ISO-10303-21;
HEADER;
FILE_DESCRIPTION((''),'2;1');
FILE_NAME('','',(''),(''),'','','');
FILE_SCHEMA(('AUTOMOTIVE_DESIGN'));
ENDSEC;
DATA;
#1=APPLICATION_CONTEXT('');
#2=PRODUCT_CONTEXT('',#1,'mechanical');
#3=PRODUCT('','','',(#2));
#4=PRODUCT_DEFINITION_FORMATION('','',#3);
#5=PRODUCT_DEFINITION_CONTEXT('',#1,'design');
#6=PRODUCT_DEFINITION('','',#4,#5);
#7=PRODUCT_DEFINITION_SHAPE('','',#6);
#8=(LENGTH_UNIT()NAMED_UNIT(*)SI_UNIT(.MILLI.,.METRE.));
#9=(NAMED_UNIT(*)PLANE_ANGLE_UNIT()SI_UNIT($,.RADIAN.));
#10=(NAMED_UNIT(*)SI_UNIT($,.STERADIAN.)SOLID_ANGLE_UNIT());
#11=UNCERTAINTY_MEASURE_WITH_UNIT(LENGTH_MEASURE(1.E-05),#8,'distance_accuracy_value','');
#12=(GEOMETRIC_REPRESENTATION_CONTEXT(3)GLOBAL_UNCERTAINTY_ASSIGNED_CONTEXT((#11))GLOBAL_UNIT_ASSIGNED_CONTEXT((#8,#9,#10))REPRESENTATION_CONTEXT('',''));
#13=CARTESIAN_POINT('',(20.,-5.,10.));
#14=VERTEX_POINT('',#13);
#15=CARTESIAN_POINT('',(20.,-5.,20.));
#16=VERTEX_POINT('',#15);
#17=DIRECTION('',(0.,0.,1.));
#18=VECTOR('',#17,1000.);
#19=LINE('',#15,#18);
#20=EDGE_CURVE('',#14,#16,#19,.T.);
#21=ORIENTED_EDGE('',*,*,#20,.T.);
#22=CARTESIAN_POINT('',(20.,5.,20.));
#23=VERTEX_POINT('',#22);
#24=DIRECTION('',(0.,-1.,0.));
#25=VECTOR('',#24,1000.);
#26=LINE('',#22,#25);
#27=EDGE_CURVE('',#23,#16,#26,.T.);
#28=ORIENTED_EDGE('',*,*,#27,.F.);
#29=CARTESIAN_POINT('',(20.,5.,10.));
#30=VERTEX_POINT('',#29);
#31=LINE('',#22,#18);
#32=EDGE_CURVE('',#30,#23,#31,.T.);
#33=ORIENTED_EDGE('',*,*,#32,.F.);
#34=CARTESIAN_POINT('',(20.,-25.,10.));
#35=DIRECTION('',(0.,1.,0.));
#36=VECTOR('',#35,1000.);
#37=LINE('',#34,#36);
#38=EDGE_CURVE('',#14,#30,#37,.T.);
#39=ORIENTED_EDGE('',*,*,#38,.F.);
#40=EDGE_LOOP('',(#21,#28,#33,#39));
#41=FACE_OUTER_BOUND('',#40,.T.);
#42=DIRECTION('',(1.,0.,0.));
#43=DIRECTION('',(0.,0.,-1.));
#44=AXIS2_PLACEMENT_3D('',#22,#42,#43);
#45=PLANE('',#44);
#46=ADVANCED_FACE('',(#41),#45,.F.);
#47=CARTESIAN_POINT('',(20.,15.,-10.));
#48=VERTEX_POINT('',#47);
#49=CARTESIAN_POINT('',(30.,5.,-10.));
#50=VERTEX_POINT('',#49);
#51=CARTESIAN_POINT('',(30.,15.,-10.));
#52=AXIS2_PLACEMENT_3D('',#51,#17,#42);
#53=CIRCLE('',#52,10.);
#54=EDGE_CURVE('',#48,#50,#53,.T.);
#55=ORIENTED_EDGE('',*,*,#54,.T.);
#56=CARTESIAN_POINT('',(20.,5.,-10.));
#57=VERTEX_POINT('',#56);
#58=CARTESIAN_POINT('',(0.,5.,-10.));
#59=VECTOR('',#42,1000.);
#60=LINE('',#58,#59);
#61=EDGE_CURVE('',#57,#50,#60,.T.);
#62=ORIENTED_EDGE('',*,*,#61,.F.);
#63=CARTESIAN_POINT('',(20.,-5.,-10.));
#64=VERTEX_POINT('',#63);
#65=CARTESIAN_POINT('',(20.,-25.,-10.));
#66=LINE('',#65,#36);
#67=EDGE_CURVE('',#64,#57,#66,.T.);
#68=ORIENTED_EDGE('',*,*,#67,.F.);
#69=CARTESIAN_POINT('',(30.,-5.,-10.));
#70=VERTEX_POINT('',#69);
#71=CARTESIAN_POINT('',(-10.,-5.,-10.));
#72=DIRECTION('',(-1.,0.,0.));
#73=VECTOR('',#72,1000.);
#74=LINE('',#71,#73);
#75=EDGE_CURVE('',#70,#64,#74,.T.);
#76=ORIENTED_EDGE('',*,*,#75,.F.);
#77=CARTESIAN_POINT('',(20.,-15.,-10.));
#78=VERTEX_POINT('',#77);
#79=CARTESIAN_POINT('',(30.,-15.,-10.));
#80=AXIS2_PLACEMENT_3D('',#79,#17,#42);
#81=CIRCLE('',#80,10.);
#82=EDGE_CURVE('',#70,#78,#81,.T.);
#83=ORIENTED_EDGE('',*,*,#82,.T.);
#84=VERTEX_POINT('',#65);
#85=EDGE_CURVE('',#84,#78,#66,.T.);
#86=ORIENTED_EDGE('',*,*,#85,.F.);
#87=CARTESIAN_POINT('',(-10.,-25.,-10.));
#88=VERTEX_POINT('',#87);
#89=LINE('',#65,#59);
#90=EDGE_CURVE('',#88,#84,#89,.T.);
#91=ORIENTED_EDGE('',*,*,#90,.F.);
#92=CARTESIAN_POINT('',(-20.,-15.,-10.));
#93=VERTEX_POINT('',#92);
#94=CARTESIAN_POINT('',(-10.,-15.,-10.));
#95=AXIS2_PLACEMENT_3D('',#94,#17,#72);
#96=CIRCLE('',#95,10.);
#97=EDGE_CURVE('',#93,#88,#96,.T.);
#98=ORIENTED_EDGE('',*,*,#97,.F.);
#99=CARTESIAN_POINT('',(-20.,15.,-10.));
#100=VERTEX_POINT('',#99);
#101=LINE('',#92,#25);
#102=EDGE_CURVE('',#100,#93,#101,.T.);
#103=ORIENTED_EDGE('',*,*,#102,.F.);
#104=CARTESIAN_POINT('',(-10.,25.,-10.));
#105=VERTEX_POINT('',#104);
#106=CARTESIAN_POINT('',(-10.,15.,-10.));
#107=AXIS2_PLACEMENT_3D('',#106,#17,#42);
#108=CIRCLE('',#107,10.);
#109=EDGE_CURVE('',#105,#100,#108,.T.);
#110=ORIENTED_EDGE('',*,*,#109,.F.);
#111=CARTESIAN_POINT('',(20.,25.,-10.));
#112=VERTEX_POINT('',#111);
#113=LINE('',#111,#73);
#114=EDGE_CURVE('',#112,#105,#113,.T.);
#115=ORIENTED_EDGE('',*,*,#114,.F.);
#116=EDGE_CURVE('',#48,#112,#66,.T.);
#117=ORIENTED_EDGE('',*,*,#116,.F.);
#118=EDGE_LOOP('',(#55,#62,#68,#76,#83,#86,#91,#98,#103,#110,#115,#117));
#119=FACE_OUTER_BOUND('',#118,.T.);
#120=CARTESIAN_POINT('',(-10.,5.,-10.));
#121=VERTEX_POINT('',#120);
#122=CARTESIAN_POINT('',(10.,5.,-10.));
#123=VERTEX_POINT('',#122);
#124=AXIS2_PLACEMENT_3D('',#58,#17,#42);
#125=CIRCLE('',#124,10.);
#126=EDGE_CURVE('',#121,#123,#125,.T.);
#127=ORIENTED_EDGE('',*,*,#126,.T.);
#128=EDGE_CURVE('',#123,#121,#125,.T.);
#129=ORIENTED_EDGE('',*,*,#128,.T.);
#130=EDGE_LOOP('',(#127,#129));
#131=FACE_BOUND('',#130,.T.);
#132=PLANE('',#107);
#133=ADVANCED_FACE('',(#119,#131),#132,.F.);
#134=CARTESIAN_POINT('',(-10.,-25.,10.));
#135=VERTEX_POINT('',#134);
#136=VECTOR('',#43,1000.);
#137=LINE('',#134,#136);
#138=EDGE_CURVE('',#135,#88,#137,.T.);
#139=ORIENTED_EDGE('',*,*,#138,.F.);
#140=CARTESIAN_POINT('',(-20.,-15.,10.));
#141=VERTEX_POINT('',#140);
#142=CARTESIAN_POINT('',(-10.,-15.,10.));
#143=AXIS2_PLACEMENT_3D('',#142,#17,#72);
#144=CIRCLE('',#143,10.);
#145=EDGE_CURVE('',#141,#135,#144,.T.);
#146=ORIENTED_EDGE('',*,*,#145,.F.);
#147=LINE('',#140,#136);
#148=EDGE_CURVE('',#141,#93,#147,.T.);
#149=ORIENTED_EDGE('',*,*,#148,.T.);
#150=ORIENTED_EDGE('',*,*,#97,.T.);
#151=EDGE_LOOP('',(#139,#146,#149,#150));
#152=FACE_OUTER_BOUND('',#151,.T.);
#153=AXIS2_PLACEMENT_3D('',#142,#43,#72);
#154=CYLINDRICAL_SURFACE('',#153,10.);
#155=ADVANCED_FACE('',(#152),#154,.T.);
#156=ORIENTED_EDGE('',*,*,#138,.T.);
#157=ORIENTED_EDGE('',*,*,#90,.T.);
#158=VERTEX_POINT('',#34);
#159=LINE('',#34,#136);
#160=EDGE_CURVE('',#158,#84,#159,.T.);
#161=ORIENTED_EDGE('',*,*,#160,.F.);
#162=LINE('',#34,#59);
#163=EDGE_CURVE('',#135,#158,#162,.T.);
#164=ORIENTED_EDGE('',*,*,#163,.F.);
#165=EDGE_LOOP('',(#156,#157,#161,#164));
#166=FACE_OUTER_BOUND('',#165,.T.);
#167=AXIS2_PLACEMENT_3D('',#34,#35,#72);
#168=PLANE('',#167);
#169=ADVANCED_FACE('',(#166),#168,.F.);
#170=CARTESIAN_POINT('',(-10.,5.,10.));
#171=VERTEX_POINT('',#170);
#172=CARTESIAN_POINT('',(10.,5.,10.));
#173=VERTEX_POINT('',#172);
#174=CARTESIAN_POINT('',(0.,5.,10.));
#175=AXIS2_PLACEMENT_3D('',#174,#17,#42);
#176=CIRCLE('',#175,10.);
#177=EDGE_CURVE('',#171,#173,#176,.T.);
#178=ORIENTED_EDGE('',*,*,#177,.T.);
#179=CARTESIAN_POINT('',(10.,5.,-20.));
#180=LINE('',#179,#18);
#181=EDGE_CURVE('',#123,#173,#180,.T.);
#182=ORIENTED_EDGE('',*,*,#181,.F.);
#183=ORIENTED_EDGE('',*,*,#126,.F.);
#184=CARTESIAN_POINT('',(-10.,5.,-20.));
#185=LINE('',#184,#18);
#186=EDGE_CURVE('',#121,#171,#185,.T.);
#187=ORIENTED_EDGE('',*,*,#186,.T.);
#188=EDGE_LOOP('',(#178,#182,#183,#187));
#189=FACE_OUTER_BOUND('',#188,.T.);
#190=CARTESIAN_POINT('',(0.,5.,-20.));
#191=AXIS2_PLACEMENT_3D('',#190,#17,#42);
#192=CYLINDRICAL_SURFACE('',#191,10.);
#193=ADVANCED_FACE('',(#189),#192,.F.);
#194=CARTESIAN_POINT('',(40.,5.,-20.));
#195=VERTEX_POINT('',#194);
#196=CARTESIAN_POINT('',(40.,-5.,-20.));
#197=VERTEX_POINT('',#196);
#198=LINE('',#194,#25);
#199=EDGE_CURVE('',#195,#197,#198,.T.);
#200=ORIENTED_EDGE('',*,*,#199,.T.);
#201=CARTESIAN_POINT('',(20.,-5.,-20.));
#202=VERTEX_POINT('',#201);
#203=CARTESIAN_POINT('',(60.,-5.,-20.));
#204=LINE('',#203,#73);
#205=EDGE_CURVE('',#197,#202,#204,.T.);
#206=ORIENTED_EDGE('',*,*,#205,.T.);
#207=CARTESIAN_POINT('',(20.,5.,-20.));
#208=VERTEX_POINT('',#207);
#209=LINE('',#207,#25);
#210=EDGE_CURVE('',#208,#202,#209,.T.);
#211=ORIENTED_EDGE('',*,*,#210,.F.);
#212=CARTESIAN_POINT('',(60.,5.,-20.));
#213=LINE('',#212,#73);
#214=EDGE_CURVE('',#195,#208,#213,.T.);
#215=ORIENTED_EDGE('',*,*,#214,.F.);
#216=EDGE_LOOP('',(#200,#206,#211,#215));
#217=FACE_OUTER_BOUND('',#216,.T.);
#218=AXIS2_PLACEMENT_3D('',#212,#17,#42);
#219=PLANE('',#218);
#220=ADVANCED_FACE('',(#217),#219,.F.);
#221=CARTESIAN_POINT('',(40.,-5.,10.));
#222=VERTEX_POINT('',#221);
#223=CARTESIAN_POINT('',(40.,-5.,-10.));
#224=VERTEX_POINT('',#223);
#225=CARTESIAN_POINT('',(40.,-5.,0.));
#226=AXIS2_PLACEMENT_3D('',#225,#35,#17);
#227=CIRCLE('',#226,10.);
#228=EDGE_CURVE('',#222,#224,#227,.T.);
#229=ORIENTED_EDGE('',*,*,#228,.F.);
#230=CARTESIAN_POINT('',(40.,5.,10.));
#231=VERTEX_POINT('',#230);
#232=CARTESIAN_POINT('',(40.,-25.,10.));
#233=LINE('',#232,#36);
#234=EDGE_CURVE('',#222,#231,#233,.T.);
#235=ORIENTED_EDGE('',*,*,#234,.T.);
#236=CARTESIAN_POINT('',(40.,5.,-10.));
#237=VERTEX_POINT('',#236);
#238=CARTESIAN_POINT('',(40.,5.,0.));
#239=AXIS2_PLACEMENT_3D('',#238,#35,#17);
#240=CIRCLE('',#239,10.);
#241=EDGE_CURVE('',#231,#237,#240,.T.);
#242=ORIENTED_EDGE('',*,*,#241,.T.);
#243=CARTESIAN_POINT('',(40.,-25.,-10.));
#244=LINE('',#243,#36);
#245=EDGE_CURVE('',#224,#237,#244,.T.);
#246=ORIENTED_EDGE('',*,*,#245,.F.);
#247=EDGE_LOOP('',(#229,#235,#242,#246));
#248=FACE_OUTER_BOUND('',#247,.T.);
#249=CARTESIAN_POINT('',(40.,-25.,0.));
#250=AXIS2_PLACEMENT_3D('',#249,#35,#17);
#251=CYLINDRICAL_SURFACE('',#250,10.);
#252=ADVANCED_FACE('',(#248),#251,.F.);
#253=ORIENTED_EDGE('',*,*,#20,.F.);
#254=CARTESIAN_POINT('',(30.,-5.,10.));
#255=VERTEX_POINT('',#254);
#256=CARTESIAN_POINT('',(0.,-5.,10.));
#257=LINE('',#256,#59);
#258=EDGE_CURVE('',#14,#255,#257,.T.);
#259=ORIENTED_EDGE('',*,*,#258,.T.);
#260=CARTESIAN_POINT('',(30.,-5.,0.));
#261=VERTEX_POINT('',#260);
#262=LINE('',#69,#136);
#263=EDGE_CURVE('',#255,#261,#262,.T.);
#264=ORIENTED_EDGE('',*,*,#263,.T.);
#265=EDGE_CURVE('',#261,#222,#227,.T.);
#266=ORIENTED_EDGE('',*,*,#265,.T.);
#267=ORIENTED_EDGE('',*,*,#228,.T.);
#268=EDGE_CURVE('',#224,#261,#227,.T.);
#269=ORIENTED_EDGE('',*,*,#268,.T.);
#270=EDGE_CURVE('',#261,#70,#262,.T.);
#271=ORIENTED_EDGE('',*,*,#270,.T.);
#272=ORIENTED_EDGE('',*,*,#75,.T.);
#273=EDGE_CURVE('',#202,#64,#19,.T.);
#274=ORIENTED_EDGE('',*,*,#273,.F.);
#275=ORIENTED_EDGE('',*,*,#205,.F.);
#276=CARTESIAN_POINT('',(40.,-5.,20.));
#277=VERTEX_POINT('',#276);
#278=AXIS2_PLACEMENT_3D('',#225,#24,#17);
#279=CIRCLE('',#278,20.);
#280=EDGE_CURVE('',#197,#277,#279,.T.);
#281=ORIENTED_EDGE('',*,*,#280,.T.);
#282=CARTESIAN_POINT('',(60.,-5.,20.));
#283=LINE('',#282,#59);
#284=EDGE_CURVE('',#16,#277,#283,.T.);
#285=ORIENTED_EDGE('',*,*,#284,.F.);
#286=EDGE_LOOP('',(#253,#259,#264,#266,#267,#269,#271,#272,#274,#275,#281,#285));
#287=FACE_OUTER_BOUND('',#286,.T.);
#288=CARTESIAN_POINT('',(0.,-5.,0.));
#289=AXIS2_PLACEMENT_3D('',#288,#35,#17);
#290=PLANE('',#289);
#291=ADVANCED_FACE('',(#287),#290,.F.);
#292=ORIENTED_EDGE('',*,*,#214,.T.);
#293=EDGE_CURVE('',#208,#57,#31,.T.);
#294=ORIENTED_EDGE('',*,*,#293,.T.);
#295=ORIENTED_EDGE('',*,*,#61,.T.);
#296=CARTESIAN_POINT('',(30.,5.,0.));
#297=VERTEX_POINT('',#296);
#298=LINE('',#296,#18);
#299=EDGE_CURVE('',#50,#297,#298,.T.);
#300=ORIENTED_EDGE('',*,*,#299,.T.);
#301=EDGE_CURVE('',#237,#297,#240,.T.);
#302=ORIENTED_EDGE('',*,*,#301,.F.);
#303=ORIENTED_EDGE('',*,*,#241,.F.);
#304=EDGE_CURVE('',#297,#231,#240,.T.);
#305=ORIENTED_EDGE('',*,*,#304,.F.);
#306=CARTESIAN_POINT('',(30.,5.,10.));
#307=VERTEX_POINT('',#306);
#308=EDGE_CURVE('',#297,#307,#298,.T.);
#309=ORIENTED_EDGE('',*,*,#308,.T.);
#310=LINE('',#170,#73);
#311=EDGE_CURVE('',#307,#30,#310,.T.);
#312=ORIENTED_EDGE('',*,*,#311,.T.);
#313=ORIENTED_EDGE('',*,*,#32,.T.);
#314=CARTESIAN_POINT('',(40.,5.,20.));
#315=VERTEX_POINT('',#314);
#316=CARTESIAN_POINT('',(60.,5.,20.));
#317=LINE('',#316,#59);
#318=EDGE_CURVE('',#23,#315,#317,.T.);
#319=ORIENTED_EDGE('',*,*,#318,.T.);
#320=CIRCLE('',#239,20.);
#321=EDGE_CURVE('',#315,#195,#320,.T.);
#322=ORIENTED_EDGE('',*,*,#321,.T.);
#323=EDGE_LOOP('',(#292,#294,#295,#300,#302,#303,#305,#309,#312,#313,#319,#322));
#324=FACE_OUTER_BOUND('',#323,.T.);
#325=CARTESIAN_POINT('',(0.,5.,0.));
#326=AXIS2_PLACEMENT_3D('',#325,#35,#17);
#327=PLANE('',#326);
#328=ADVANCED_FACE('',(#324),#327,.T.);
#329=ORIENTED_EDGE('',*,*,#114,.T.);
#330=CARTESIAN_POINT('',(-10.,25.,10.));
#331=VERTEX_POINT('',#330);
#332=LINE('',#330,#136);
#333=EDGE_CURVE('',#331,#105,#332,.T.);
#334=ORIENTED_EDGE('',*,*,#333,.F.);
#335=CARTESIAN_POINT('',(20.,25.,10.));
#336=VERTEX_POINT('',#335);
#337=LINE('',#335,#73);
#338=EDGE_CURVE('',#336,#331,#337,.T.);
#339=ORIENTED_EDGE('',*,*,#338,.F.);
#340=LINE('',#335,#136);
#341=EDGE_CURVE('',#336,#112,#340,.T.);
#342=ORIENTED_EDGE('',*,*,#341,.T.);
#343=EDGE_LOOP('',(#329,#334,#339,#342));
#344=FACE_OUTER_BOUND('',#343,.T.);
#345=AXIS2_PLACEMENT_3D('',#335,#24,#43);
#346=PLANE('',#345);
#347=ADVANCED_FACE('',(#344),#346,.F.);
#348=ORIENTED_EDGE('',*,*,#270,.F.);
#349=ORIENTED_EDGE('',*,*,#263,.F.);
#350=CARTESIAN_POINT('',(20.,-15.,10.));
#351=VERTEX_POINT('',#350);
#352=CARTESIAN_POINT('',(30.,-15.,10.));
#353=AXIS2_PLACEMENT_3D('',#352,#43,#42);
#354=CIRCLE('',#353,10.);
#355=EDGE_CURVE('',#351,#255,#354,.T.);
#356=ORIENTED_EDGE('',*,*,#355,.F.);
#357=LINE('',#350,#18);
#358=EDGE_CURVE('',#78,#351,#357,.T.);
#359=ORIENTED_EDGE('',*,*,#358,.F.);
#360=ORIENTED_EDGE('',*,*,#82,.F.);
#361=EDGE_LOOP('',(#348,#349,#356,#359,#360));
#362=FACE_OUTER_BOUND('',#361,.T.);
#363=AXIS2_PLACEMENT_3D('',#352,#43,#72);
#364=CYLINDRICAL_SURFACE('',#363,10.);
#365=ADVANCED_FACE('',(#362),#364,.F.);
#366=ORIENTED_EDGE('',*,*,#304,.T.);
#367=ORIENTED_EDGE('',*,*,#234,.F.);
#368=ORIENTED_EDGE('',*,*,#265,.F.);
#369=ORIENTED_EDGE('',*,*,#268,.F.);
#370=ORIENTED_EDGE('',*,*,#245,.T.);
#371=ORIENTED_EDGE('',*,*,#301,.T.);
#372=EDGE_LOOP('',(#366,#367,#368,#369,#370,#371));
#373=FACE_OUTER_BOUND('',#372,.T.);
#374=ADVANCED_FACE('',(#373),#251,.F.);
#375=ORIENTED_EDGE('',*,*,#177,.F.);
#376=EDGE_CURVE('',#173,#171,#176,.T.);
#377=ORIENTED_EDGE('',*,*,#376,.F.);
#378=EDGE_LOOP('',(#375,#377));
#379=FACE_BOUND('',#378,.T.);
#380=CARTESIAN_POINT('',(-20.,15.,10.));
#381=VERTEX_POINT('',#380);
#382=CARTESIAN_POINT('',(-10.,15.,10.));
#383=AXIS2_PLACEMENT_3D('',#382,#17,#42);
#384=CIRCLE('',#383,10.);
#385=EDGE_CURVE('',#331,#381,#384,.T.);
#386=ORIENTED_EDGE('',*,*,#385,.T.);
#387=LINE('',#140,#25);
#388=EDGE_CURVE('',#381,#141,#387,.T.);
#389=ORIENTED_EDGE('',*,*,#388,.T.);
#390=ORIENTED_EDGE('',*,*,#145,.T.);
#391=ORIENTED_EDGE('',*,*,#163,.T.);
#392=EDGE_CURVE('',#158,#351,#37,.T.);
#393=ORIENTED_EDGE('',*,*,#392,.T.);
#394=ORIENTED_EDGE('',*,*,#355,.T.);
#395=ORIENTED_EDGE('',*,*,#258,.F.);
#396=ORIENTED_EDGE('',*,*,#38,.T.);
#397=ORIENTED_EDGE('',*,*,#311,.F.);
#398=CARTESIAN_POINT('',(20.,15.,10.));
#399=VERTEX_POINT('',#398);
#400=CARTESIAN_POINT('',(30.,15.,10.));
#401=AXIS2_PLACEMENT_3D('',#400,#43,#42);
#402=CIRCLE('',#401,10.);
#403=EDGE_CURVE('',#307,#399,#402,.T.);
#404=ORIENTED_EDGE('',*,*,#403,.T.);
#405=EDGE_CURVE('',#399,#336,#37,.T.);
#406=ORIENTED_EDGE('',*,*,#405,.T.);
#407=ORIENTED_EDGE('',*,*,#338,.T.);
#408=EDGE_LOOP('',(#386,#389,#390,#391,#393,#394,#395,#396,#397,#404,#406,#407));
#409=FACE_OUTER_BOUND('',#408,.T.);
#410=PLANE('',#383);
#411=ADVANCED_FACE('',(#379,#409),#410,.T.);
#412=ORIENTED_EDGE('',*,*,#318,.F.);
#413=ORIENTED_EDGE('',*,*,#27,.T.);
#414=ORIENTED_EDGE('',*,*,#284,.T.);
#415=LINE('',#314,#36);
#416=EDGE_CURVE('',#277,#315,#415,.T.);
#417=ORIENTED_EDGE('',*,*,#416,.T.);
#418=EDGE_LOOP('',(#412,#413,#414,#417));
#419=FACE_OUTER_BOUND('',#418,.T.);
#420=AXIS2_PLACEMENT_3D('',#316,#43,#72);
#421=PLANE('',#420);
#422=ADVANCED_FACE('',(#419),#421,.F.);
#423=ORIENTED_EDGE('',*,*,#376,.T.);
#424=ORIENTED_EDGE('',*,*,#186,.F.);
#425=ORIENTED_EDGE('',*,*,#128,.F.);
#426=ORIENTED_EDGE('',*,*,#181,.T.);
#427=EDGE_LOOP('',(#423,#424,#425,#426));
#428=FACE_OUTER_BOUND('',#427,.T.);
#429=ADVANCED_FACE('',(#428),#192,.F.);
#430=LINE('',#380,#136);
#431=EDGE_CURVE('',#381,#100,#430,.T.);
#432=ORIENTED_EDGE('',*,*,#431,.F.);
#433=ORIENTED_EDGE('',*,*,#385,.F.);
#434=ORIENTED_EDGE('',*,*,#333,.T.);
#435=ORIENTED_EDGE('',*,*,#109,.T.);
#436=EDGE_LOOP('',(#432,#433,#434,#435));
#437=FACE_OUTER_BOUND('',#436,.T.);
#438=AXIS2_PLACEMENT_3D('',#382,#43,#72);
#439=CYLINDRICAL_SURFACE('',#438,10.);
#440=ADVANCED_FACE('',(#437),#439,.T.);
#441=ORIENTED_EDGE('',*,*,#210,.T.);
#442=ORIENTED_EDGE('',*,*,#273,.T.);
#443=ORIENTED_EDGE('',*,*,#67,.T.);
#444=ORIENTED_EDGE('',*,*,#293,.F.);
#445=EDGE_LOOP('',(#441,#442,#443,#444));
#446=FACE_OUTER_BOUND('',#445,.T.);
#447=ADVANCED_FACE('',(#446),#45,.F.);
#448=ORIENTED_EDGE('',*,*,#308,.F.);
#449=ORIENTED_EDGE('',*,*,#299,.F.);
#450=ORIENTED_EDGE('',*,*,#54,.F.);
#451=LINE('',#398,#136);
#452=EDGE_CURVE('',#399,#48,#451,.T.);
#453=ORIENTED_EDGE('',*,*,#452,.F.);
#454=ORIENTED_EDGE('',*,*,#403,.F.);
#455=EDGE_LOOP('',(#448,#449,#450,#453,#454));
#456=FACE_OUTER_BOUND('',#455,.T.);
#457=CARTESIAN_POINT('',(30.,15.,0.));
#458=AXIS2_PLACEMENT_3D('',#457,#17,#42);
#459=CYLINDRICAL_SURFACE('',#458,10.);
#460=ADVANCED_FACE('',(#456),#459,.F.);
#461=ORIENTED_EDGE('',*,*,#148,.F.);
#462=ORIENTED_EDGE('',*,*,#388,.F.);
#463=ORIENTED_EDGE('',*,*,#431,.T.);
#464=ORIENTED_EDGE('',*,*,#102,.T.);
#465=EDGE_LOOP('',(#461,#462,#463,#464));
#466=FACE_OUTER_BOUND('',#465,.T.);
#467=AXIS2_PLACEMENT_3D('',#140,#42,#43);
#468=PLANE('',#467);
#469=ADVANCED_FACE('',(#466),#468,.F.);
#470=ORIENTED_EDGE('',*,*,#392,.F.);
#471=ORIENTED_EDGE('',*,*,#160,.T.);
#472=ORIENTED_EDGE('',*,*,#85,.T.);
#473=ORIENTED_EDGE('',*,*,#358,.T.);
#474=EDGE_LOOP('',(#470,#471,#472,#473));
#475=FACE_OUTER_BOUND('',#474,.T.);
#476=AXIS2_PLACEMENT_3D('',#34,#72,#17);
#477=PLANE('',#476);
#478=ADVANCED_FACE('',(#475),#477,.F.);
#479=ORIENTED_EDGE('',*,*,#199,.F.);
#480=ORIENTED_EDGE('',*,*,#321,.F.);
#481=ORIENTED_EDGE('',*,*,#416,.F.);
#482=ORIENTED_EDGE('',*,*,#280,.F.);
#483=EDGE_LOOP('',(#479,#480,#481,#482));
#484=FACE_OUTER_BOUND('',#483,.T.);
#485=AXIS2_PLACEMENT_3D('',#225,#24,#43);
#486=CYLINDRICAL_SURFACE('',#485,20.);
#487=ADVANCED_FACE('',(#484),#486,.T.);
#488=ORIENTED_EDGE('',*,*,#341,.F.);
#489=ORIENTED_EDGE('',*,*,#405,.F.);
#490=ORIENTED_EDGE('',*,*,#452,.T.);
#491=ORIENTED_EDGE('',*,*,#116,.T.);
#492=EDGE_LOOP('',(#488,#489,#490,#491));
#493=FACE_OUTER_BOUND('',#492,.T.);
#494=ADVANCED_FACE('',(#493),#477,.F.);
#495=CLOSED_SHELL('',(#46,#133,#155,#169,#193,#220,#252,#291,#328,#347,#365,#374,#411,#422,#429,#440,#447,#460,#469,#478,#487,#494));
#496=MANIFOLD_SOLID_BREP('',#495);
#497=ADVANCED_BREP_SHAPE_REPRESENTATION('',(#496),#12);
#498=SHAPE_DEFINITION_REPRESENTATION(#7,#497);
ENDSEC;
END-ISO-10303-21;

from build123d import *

# Parameters (mm, degrees)
BASE_BLOCK_DEPTH           = 10
LUG_TAB_PROFILE_W          = 40
LUG_TAB_PROFILE_H          = 40
LUG_TAB_DEPTH              = 5
LUG_TAB_EDGE_FILLET_RADIUS = 20
LUG_TAB_EDGE_FILLET_LENGTH = 10
CORNER_FILLET_R10_R        = 10
CROSS_HOLE_PROFILE_R       = 10
CROSS_HOLE_20_DEPTH        = 72.589105316
LUG_HOLE_PROFILE_R         = 10
LUG_HOLE_20_DEPTH          = 71


with BuildPart() as part:
    # Base Block Profile → Base Block (new, symmetric)
    with BuildSketch(Plane.XY):
        with BuildLine():
            Line((20, -25), (-10, -25))
            ThreePointArc((-10, -25), (-17.071067812, -22.071067812), (-20, -15))
            Line((-20, -15), (-20, 15))
            ThreePointArc((-20, 15), (-17.071067812, 22.071067812), (-10, 25))
            Line((-10, 25), (20, 25))
            Line((20, 25), (20, -25))
        make_face()
    extrude(amount=BASE_BLOCK_DEPTH, both=True)

    # Lug Tab Profile → Lug Tab (add, symmetric)
    with BuildSketch(Plane(origin=(0, 0, 0), x_dir=(1, 0, 0), z_dir=(0, 1, 0))):
        with Locations((40, 0)):
            Rectangle(LUG_TAB_PROFILE_W, LUG_TAB_PROFILE_H)
    extrude(amount=LUG_TAB_DEPTH, both=True)

    # Lug Tab Edge Fillet: full round fillet: the end face becomes a half cylinder, R = half its width
    lug_tab_edge_fillet_face = Plane((60, 0, 0), x_dir=(0, -1, 0), z_dir=(1, 0, 0))  # on the end face: x along it, z out of the body
    lug_tab_edge_fillet_slab = lug_tab_edge_fillet_face.offset(-LUG_TAB_EDGE_FILLET_RADIUS / 2) * Box(LUG_TAB_EDGE_FILLET_LENGTH, 2 * LUG_TAB_EDGE_FILLET_RADIUS, LUG_TAB_EDGE_FILLET_RADIUS, mode=Mode.PRIVATE)  # the body's end, R deep
    lug_tab_edge_fillet_round = Plane((40, 0, 0), x_dir=(1, 0, 0), z_dir=(0, -1, 0)) * Cylinder(LUG_TAB_EDGE_FILLET_RADIUS, LUG_TAB_EDGE_FILLET_LENGTH, mode=Mode.PRIVATE)  # its axis R under the face
    add(lug_tab_edge_fillet_slab - lug_tab_edge_fillet_round, mode=Mode.SUBTRACT)

    # Corner Fillet R10
    corner_fillet_r10_edges = [part.edges().sort_by_distance(p)[0] for p in [
        (20, 5, 0),
        (20, -5, 0),
    ]]
    fillet(corner_fillet_r10_edges, radius=CORNER_FILLET_R10_R)

    # Cross Hole Profile → Cross Hole _20 (cut, through all)
    with BuildSketch(Plane.XY.offset(10)):
        with Locations((0, 5)):
            Circle(CROSS_HOLE_PROFILE_R)
    extrude(amount=-CROSS_HOLE_20_DEPTH, mode=Mode.SUBTRACT)

    # Lug Hole Profile → Lug Hole _20 (cut, through all)
    with BuildSketch(Plane(origin=(0, 5, 0), x_dir=(1, 0, 0), z_dir=(0, 1, 0))):
        with Locations(Location((40, 0, 0), (0, 0, 180))):
            Circle(LUG_HOLE_PROFILE_R)
    extrude(amount=-LUG_HOLE_20_DEPTH, mode=Mode.SUBTRACT)


solid = part.part
